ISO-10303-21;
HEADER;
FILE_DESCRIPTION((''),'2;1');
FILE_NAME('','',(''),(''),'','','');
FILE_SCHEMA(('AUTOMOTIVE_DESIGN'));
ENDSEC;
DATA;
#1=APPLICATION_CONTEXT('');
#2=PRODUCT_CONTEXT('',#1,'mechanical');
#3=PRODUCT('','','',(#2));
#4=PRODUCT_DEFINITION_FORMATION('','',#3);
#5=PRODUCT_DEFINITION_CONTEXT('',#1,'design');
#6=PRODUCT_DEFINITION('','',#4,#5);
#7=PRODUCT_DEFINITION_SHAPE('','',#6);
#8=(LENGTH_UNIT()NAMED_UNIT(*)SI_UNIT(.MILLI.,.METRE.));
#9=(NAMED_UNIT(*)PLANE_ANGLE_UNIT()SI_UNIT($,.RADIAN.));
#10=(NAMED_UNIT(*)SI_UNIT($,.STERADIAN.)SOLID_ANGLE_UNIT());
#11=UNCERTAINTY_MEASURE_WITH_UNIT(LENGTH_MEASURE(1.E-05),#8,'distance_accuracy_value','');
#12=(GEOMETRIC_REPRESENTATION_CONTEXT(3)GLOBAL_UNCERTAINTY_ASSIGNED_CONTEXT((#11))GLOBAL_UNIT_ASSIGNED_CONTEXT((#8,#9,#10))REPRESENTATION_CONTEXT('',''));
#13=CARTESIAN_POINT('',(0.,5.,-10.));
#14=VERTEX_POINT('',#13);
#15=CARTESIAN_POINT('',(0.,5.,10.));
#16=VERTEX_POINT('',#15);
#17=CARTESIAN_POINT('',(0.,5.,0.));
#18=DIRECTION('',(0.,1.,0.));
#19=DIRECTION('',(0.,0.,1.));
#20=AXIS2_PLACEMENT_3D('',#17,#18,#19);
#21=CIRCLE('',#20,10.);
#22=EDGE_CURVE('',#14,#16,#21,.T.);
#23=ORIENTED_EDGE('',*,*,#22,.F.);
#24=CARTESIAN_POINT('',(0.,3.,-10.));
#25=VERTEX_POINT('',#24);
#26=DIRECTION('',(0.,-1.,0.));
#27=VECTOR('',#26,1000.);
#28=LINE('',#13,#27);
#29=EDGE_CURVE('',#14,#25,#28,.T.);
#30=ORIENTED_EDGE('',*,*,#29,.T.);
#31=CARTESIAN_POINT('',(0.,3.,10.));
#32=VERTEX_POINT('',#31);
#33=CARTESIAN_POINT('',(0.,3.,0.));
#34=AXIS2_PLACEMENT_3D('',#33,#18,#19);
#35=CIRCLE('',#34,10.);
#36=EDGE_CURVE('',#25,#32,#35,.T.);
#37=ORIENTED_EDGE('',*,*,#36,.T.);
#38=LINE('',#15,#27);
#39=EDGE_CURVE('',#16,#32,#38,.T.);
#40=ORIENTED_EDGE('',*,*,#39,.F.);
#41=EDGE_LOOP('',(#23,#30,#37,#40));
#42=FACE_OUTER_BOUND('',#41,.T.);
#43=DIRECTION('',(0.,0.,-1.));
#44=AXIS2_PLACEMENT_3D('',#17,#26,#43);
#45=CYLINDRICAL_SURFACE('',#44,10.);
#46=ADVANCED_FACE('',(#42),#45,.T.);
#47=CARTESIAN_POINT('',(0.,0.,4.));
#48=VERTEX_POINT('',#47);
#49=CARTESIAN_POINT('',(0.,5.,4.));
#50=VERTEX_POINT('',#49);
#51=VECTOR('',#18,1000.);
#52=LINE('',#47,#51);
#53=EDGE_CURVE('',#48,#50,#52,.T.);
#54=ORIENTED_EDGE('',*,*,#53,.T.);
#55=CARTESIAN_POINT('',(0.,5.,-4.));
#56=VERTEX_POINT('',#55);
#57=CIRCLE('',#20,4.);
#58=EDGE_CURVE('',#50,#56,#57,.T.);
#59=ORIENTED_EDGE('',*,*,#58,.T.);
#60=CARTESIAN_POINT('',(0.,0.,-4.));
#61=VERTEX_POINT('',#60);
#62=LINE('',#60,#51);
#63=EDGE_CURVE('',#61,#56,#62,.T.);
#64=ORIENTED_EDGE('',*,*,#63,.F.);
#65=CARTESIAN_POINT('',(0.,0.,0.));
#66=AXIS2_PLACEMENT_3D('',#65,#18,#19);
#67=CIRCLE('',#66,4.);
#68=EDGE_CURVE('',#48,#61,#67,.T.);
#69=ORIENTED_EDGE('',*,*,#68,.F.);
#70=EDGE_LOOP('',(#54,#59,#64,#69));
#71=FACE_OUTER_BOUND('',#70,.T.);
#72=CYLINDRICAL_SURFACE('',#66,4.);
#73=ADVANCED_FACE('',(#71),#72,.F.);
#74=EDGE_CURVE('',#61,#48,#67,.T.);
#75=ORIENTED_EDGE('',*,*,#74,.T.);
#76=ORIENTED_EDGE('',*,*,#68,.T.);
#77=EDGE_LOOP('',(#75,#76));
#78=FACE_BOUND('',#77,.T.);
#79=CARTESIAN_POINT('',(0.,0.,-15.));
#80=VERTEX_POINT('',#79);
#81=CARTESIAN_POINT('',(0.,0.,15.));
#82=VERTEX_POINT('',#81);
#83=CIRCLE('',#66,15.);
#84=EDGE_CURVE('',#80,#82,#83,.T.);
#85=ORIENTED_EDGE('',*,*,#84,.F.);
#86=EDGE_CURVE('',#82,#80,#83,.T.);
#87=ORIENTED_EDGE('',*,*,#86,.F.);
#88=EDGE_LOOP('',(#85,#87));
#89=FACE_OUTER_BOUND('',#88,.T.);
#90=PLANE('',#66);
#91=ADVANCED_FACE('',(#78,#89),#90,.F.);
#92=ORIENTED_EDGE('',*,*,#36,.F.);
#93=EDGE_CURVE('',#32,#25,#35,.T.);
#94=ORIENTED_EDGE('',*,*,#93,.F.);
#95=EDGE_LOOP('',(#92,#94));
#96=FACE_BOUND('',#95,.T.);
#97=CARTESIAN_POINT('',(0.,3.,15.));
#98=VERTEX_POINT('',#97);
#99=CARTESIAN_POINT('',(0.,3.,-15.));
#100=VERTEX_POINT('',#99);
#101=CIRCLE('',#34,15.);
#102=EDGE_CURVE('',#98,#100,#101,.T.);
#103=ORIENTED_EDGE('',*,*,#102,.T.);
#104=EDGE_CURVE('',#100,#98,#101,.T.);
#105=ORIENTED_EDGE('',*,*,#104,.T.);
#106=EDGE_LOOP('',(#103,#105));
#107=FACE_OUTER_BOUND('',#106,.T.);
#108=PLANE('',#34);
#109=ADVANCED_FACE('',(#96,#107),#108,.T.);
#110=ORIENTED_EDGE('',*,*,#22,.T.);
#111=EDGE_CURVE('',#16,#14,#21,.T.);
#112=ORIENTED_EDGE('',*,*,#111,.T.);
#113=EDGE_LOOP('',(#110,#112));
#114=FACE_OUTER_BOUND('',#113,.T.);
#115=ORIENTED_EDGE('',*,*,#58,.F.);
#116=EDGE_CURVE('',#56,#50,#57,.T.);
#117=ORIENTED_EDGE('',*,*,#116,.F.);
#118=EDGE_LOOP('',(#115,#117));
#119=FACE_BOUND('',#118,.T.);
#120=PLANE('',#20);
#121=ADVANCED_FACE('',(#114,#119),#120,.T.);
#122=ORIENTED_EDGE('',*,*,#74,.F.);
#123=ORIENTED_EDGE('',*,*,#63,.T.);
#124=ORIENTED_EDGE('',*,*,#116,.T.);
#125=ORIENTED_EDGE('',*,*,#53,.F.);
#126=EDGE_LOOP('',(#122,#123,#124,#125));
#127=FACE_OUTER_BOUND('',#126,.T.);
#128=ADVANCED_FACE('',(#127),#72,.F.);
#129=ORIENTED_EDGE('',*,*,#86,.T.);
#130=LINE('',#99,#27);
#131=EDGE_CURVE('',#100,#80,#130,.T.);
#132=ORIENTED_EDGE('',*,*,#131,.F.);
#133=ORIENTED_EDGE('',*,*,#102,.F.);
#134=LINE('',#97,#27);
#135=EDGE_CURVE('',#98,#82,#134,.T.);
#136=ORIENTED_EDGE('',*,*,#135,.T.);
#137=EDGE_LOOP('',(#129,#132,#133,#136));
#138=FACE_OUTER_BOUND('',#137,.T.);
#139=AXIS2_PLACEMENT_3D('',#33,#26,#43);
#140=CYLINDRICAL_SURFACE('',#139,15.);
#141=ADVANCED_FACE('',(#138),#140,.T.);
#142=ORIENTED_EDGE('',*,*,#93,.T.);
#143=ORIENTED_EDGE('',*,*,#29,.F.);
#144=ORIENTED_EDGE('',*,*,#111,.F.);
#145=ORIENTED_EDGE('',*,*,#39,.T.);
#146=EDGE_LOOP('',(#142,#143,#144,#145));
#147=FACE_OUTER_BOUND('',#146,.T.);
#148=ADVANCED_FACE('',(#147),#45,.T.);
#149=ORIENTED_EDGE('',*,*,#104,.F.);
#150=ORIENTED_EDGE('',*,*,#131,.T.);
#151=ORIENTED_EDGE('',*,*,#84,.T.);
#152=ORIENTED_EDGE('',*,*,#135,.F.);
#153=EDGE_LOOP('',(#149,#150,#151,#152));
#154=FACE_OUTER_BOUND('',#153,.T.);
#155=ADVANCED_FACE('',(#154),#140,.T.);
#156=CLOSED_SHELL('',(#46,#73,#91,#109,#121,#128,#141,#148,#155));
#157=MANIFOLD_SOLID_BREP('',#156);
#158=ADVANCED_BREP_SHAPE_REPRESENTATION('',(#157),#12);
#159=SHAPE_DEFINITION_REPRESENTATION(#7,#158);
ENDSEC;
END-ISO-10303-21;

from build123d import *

# Parameters (mm, degrees)
SKETCH_1_R          = 15
EXTRUDE_1_DEPTH     = 3
SKETCH_2_R          = 10
EXTRUDE_2_DEPTH     = 2
SKETCH_3_R          = 4
CUT_EXTRUDE_1_DEPTH = 22.794494718


with BuildPart() as part:
    # 草图1 → 凸台-拉伸1 (new body)
    with BuildSketch(Plane(origin=(0, 0, 0), x_dir=(1, 0, 0), z_dir=(0, 1, 0))):
        with Locations(Location((0, 0, 0), (0, 0, 270))):
            Circle(SKETCH_1_R)
    extrude(amount=EXTRUDE_1_DEPTH)

    # 草图2 → 凸台-拉伸2 (add)
    with BuildSketch(Plane(origin=(0, 3, 0), x_dir=(1, 0, 0), z_dir=(0, 1, 0))):
        with Locations(Location((0, 0, 0), (0, 0, 270))):
            Circle(SKETCH_2_R)
    extrude(amount=EXTRUDE_2_DEPTH)

    # 草图3 → 切除-拉伸1 (cut, through all)
    with BuildSketch(Plane(origin=(0, 5, 0), x_dir=(1, 0, 0), z_dir=(0, 1, 0))):
        with Locations(Location((0, 0, 0), (0, 0, 270))):
            Circle(SKETCH_3_R)
    extrude(amount=-CUT_EXTRUDE_1_DEPTH, mode=Mode.SUBTRACT)


solid = part.part
